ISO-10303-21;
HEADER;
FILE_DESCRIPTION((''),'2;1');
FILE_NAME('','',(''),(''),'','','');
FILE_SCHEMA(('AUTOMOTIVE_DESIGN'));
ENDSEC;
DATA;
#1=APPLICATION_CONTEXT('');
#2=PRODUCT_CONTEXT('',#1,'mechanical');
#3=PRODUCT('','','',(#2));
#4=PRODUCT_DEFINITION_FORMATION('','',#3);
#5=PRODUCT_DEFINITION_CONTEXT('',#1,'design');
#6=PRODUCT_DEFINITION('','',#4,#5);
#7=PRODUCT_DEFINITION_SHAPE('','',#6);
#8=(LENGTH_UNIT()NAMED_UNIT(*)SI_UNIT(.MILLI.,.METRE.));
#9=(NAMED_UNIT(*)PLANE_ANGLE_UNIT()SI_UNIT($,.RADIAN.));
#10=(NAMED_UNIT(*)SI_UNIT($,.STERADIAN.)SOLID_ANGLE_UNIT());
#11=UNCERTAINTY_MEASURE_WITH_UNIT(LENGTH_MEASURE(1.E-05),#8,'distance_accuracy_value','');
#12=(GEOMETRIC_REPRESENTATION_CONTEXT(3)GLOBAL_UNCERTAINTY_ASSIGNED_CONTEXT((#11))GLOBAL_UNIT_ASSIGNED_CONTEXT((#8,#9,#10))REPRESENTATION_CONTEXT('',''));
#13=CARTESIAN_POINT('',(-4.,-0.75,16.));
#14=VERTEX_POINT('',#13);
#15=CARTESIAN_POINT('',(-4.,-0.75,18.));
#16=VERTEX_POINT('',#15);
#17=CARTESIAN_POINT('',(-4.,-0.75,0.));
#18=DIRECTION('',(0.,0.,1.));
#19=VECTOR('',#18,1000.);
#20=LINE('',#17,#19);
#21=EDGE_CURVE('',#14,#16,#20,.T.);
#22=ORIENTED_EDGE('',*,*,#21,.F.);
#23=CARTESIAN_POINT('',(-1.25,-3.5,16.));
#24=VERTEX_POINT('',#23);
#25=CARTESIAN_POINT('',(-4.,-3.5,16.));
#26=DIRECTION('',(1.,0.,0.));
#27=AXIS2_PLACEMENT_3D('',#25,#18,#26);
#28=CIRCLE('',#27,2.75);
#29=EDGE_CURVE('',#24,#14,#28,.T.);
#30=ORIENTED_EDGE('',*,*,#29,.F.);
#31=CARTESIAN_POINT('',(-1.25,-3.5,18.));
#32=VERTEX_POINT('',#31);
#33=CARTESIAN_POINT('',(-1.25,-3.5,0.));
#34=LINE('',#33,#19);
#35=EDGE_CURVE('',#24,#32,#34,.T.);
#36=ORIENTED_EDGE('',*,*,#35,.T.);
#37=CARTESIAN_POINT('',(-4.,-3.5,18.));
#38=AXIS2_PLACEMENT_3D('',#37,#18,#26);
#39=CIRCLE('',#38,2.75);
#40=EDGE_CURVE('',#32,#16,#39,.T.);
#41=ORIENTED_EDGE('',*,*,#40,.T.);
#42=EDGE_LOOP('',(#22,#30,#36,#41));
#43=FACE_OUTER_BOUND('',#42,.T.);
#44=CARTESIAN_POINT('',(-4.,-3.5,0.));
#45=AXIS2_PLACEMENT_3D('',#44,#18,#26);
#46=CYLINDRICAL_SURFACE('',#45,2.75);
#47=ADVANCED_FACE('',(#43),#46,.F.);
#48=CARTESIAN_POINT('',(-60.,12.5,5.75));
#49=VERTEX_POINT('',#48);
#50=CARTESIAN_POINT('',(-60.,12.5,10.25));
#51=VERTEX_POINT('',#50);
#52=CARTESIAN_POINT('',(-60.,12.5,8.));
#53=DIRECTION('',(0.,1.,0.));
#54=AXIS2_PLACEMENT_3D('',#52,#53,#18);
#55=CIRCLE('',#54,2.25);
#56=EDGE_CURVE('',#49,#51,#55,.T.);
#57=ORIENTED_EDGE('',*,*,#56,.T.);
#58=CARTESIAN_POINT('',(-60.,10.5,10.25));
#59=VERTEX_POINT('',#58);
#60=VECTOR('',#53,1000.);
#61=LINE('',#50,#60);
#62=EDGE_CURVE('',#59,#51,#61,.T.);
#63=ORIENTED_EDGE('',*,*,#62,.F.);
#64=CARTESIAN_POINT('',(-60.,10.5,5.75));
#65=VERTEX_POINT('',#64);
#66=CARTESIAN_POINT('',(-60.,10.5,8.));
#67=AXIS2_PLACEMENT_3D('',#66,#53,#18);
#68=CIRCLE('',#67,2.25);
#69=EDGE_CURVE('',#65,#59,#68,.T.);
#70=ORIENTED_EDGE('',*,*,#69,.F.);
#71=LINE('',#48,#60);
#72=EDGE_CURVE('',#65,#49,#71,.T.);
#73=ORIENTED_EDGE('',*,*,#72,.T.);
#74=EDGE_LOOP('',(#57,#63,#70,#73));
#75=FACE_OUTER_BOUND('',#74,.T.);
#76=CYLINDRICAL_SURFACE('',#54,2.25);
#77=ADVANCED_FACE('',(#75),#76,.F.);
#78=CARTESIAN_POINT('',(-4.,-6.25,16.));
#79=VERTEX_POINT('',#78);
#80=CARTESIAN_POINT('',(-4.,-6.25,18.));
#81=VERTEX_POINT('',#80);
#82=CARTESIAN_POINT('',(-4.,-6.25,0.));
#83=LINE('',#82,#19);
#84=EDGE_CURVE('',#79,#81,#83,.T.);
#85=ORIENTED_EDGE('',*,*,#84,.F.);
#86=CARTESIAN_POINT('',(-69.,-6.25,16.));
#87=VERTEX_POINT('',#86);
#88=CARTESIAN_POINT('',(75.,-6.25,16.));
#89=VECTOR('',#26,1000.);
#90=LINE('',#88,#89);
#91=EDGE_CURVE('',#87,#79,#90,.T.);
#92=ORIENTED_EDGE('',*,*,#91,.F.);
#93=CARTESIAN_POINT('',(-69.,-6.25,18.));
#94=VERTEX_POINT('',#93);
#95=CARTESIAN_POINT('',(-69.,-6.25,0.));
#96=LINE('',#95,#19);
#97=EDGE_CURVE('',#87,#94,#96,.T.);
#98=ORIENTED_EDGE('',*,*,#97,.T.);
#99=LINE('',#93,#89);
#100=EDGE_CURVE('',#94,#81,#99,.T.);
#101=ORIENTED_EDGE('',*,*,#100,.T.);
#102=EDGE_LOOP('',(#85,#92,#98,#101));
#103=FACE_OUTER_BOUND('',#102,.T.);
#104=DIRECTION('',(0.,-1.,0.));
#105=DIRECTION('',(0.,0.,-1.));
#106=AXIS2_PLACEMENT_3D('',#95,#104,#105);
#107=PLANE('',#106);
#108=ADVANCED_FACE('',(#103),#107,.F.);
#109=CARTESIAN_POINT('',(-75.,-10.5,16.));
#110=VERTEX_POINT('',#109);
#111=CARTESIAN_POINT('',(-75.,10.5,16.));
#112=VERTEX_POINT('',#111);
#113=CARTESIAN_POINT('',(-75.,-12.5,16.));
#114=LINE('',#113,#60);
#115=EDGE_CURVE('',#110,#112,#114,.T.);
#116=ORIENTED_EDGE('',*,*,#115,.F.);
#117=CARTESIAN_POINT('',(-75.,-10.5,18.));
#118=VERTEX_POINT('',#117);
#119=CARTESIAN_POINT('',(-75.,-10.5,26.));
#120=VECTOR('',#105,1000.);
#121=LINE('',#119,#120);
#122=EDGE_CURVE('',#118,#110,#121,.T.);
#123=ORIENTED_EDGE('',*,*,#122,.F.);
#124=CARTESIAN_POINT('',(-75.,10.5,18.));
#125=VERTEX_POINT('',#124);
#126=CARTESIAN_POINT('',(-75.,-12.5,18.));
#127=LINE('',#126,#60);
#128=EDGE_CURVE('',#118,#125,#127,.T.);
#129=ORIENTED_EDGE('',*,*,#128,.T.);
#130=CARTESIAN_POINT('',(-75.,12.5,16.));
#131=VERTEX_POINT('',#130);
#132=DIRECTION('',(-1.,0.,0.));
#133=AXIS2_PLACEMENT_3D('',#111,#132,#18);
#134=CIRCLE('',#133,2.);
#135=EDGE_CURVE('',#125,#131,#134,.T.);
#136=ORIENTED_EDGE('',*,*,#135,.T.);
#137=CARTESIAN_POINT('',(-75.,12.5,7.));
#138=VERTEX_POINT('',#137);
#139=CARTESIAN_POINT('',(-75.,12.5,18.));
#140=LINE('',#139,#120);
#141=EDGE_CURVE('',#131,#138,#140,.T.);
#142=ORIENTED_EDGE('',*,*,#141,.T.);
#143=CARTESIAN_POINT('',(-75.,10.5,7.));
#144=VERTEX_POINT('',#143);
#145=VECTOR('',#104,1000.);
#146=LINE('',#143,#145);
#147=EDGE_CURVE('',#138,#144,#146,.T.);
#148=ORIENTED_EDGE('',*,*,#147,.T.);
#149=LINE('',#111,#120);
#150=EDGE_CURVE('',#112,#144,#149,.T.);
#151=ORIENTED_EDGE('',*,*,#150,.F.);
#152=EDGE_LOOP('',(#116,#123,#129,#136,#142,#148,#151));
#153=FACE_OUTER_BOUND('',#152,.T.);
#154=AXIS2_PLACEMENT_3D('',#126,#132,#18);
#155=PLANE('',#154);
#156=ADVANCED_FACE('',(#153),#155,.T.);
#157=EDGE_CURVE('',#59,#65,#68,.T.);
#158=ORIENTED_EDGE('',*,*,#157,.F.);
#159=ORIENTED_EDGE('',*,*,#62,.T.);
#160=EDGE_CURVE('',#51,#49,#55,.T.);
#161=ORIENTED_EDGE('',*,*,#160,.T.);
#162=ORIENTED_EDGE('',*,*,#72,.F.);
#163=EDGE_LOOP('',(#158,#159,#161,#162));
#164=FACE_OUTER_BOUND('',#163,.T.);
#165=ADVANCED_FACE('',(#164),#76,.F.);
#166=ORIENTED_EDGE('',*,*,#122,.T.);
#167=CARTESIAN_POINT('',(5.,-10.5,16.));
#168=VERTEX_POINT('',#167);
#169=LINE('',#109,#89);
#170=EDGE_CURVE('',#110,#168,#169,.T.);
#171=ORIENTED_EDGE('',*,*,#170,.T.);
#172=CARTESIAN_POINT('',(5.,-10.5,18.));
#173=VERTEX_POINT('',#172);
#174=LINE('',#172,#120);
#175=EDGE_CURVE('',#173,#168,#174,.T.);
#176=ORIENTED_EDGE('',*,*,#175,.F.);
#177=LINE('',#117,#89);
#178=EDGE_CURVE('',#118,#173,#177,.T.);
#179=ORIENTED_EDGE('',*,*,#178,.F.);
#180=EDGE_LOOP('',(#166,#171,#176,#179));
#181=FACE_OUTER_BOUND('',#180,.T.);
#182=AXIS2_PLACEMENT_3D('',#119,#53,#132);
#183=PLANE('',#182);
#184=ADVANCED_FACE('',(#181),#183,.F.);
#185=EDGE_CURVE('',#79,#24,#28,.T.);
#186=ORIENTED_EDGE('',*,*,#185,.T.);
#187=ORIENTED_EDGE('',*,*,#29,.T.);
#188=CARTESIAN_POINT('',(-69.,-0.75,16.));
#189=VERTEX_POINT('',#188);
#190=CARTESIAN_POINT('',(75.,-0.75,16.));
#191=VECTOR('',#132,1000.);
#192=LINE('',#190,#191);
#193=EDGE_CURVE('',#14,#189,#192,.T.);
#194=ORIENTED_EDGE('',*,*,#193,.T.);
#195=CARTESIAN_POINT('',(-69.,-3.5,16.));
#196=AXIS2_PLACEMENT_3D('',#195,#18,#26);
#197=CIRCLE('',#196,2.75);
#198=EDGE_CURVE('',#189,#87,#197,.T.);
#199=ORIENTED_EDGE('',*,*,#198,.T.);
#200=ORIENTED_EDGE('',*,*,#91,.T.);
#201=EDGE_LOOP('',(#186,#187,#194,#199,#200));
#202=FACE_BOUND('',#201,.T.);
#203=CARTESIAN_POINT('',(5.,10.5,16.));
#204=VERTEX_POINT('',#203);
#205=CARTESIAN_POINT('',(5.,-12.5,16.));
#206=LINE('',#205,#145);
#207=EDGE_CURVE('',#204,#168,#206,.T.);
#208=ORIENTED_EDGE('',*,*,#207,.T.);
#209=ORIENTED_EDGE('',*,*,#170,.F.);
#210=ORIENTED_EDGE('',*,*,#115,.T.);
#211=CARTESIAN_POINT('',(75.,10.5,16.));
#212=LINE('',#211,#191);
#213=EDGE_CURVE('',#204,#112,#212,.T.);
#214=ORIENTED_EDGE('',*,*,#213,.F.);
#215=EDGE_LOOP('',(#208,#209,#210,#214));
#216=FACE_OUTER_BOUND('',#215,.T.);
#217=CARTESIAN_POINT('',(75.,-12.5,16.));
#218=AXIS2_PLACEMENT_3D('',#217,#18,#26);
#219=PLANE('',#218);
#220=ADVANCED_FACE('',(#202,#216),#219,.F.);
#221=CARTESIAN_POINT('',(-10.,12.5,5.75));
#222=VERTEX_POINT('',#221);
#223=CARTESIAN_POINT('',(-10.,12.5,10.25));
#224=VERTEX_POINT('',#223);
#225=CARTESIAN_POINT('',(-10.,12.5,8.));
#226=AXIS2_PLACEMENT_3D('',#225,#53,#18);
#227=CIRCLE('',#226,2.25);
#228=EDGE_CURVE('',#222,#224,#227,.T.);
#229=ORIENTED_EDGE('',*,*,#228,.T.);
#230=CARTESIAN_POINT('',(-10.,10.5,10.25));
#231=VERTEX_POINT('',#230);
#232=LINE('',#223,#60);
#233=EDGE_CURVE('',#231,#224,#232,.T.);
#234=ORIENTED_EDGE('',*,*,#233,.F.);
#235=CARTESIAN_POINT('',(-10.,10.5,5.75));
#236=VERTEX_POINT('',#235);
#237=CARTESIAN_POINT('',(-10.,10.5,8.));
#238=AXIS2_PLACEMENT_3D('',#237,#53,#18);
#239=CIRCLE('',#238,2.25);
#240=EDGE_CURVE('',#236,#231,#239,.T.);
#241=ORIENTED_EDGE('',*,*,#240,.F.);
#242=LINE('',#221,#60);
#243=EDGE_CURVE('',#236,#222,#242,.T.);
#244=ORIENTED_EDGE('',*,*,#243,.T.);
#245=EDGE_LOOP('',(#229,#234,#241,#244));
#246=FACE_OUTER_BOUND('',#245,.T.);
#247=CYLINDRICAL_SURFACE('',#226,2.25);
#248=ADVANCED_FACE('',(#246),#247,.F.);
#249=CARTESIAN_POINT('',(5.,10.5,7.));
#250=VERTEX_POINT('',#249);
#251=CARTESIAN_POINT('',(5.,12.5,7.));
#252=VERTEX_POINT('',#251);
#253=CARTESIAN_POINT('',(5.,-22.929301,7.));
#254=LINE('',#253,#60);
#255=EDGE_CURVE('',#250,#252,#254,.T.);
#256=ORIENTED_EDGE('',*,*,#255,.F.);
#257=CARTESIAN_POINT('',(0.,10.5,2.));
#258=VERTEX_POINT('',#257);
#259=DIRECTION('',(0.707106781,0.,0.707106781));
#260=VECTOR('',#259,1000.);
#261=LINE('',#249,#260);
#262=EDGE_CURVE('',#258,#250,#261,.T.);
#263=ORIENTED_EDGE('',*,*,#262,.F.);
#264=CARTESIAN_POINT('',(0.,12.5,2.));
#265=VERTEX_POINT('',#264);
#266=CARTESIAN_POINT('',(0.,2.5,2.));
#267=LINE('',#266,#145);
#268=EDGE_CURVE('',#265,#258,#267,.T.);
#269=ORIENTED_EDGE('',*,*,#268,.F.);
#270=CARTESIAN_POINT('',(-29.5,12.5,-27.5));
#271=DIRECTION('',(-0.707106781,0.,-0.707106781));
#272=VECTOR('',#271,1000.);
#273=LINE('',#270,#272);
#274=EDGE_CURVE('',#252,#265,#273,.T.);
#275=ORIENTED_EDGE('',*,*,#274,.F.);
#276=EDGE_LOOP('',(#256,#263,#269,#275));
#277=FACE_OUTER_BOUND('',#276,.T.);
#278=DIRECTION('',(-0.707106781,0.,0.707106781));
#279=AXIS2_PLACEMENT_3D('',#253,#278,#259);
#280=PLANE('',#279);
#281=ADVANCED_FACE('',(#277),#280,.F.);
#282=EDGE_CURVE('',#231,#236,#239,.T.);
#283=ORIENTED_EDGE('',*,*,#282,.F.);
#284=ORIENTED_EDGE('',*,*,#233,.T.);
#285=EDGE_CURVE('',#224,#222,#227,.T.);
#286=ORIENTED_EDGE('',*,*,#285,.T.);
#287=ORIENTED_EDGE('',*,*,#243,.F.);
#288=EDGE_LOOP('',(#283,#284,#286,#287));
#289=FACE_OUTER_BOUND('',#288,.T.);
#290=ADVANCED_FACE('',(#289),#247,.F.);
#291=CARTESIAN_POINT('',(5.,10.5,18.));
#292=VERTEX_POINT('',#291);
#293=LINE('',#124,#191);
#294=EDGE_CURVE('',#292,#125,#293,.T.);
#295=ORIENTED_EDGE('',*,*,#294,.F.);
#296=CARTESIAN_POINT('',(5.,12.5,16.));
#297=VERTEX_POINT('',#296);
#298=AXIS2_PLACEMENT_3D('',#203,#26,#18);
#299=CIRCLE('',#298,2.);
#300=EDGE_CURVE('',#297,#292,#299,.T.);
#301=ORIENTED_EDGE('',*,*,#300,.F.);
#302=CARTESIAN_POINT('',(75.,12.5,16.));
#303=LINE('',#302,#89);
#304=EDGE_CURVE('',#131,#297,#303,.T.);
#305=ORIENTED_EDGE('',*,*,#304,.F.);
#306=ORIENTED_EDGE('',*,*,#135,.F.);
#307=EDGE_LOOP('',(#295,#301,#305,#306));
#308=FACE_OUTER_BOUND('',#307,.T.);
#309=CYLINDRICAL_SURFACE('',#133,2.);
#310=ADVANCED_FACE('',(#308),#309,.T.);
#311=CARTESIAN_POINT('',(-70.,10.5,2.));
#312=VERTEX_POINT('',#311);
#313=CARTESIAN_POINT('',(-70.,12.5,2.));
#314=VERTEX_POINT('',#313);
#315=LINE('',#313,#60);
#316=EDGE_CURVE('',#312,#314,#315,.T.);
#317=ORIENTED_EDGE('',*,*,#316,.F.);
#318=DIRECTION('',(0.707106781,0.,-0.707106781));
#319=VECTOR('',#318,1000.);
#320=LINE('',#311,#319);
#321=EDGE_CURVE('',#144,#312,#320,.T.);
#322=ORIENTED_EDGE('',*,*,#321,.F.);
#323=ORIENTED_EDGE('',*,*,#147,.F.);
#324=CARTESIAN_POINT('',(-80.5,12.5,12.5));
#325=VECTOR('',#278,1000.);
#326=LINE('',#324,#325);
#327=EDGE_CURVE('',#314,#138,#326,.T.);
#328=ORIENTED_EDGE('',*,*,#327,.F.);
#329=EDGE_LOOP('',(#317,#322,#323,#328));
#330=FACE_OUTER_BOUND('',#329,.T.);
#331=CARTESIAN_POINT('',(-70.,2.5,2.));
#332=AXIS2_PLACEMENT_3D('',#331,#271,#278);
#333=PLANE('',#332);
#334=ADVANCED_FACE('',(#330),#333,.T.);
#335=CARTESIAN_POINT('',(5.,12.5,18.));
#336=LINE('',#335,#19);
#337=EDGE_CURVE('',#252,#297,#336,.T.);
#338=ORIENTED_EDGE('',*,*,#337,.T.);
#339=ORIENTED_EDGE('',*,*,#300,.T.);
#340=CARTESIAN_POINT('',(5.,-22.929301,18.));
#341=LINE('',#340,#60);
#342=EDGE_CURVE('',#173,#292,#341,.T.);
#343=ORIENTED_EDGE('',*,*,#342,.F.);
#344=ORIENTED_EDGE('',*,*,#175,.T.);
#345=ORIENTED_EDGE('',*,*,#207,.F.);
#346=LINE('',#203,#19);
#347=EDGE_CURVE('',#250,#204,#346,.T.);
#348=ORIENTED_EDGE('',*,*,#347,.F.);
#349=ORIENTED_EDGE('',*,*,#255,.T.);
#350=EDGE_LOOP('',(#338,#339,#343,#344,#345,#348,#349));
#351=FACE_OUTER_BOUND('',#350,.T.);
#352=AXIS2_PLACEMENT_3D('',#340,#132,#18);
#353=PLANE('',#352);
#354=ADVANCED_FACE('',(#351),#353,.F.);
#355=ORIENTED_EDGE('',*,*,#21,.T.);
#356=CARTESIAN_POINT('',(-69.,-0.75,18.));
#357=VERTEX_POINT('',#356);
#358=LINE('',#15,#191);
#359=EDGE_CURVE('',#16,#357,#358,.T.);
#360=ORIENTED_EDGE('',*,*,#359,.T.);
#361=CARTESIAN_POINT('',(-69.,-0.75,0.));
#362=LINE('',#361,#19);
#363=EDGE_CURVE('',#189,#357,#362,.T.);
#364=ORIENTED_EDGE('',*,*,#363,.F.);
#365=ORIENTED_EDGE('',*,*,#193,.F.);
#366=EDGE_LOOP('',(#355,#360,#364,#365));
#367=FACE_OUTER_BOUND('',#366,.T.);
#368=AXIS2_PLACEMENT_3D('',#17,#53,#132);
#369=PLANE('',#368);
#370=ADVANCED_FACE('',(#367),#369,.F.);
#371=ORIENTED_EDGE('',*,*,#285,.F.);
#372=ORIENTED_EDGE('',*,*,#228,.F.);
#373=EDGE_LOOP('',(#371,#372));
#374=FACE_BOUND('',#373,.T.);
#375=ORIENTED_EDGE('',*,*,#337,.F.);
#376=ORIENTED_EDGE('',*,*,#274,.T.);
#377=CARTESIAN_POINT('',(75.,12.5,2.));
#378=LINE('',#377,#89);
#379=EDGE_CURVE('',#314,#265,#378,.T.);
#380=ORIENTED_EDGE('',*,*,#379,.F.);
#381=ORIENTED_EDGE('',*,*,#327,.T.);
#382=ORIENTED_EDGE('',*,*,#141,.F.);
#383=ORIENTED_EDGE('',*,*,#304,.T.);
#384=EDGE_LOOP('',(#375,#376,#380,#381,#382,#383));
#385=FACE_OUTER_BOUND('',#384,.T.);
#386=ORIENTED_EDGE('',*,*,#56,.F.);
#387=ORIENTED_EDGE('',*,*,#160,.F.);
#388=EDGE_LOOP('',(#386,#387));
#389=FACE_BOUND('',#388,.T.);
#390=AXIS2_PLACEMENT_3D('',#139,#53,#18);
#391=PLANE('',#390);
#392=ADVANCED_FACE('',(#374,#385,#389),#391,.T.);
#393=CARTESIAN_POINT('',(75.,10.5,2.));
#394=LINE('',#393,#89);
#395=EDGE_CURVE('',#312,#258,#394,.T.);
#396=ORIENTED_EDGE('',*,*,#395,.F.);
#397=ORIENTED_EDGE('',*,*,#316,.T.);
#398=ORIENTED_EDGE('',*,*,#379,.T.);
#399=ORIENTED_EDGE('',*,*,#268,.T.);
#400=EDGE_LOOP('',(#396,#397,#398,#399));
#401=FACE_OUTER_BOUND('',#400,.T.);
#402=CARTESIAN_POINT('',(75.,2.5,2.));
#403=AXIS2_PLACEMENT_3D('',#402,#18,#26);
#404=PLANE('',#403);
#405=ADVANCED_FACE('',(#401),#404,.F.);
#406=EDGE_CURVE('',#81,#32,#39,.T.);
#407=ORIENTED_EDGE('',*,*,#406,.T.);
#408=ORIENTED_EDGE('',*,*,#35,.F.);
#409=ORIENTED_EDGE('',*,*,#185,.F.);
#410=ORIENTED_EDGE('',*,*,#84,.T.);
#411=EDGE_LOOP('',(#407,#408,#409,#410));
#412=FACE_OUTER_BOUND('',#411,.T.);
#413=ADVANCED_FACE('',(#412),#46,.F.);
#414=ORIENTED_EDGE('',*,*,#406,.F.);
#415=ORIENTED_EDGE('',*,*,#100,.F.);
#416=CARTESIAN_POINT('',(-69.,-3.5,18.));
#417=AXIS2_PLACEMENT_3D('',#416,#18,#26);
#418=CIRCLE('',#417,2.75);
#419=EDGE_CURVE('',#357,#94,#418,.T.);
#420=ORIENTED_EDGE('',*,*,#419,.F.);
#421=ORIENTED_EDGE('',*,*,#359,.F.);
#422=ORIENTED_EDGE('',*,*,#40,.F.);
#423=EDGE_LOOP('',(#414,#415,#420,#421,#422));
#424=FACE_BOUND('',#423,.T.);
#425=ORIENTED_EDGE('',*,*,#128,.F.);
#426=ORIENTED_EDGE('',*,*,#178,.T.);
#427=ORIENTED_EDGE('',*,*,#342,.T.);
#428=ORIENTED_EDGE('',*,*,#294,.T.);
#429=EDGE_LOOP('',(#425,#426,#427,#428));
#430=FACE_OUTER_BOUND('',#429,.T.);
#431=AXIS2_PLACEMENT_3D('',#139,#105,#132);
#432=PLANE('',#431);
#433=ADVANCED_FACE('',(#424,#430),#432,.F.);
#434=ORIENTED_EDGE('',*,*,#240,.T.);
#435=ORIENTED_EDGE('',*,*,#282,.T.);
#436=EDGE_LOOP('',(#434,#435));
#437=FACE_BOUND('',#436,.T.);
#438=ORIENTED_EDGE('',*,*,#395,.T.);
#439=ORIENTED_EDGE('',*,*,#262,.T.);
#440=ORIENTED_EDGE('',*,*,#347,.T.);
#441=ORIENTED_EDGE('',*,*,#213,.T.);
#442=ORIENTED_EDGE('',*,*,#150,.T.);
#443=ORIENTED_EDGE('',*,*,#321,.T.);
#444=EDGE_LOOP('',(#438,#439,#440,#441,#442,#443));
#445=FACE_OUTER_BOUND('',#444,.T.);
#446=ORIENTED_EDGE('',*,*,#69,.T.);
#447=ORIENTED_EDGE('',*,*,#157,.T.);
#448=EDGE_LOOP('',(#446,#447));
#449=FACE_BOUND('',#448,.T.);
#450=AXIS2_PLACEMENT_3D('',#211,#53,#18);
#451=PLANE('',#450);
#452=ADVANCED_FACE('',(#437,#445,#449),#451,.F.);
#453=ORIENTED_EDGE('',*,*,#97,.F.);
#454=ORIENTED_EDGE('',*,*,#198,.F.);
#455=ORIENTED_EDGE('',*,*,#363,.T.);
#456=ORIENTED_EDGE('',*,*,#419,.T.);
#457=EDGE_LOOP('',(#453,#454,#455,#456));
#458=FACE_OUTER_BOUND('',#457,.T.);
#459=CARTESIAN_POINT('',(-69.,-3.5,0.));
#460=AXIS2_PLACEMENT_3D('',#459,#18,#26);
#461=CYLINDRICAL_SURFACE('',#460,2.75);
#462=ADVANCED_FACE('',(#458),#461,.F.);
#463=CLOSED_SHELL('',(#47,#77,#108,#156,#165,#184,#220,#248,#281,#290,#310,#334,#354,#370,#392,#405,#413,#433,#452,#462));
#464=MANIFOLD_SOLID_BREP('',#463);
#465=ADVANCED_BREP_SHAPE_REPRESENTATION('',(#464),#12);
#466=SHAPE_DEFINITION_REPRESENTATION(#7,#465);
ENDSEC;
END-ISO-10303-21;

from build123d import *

# Parameters (mm, degrees)
SKETCH_1_W             = 150
SKETCH_1_H             = 25
BOSS_EXTRUDE_1_DEPTH   = 18
SKETCH_2_W             = 16
SKETCH_2_H             = 23
CUT_EXTRUDE_1_DEPTH    = 152.592381075
CUT_EXTRUDE_3_DEPTH    = 79.136099212
F_4_5_4_5_HOLE_1_D     = 4.5
F_4_5_4_5_HOLE_1_DEPTH = 15
F_4_5_4_5_HOLE_1_TIP   = 1.351936393
F_4_5_4_5_HOLE_3_D     = 4.5
F_4_5_4_5_HOLE_3_DEPTH = 15
F_4_5_4_5_HOLE_3_TIP   = 1.351936393
F_4_5_4_5_HOLE_2_D     = 4.5
F_4_5_4_5_HOLE_2_DEPTH = 15
F_4_5_4_5_HOLE_2_TIP   = 1.351936393
CHAMFER_1_SIZE         = 2
FILLET_1_R             = 2
SKETCH_11_W            = 150
SKETCH_11_H            = 2
CUT_EXTRUDE_4_DEPTH    = 10
CHAMFER_4_SIZE         = 5
SKETCH_12_W            = 121.932032981
SKETCH_12_H            = 48.36827262
CUT_EXTRUDE_5_DEPTH    = 78.699742599
CHAMFER_5_SIZE         = 5
SKETCH_13_W            = 80
SKETCH_13_H            = 2
CUT_EXTRUDE_6_DEPTH    = 10


with BuildPart() as part:
    # Sketch 1 → Boss-Extrude 1 (new body)
    with BuildSketch(Plane(origin=(0, 0, 0), x_dir=(-1, 0, 0), z_dir=(0, 0, -1))):
        Rectangle(SKETCH_1_W, SKETCH_1_H)
    extrude(amount=-BOSS_EXTRUDE_1_DEPTH)

    # Sketch 2 → Cut-Extrude 1 (cut, through all)
    with BuildSketch(Plane.ZY.offset(75)):
        with Locations((8, -1)):
            Rectangle(SKETCH_2_W, SKETCH_2_H)
    extrude(amount=-CUT_EXTRUDE_1_DEPTH, mode=Mode.SUBTRACT)

    # Sketch 4 → Cut-Extrude 3 (cut, through all)
    with BuildSketch(Plane.XY.offset(18)):
        with BuildLine():
            Line((-69, -6.25), (-4, -6.25))
            ThreePointArc((-4, -6.25), (-1.25, -3.5), (-4, -0.75))
            Line((-4, -0.75), (-69, -0.75))
            ThreePointArc((-69, -0.75), (-71.75, -3.5), (-69, -6.25))
        make_face()
    extrude(amount=-CUT_EXTRUDE_3_DEPTH, mode=Mode.SUBTRACT)

    # Ø4.5 (4.5) Hole 1
    with Locations(Plane(origin=(0, 12.5, 0), x_dir=(-1, 0, 0), z_dir=(0, 1, 0))):
        with Locations((-60, 8)):
            Hole(F_4_5_4_5_HOLE_1_D / 2, depth=F_4_5_4_5_HOLE_1_DEPTH)
            with Locations((0, 0, -(F_4_5_4_5_HOLE_1_DEPTH + F_4_5_4_5_HOLE_1_TIP / 2))):  # 118° drill point
                Cone(0, F_4_5_4_5_HOLE_1_D / 2, F_4_5_4_5_HOLE_1_TIP, mode=Mode.SUBTRACT)

    # Ø4.5 (4.5) Hole 3
    with Locations(Plane(origin=(0, 12.5, 0), x_dir=(-1, 0, 0), z_dir=(0, 1, 0))):
        with Locations((60, 8)):
            Hole(F_4_5_4_5_HOLE_3_D / 2, depth=F_4_5_4_5_HOLE_3_DEPTH)
            with Locations((0, 0, -(F_4_5_4_5_HOLE_3_DEPTH + F_4_5_4_5_HOLE_3_TIP / 2))):  # 118° drill point
                Cone(0, F_4_5_4_5_HOLE_3_D / 2, F_4_5_4_5_HOLE_3_TIP, mode=Mode.SUBTRACT)

    # Ø4.5 (4.5) Hole 2
    with Locations(Plane(origin=(0, 12.5, 0), x_dir=(-1, 0, 0), z_dir=(0, 1, 0))):
        with Locations((10, 8)):
            Hole(F_4_5_4_5_HOLE_2_D / 2, depth=F_4_5_4_5_HOLE_2_DEPTH)
            with Locations((0, 0, -(F_4_5_4_5_HOLE_2_DEPTH + F_4_5_4_5_HOLE_2_TIP / 2))):  # 118° drill point
                Cone(0, F_4_5_4_5_HOLE_2_D / 2, F_4_5_4_5_HOLE_2_TIP, mode=Mode.SUBTRACT)

    # Chamfer 1
    chamfer_1_edges = [part.edges().sort_by_distance(p)[0] for p in [
        (75, -12.5, 17),
    ]]
    chamfer(chamfer_1_edges, length=CHAMFER_1_SIZE)

    # Fillet 1
    fillet_1_edges = [part.edges().sort_by_distance(p)[0] for p in [
        (0, 12.5, 18),
    ]]
    fillet(fillet_1_edges, radius=FILLET_1_R)

    # Sketch 11 → Cut-Extrude 4 (cut)
    with BuildSketch(Plane(origin=(0, 12.5, 0), x_dir=(1, 0, 0), z_dir=(0, 1, 0))):
        with Locations((0, -1)):
            Rectangle(SKETCH_11_W, SKETCH_11_H)
    extrude(amount=-CUT_EXTRUDE_4_DEPTH, mode=Mode.SUBTRACT)

    # Chamfer 4
    chamfer_4_edges = [part.edges().sort_by_distance(p)[0] for p in [
        (75, 11.5, 2),
        (-75, 11.5, 2),
    ]]
    chamfer(chamfer_4_edges, length=CHAMFER_4_SIZE)

    # Sketch 12 → Cut-Extrude 5 (cut, through all)
    with BuildSketch(Plane(origin=(0, 0, 2), x_dir=(-1, 0, 0), z_dir=(0, 0, -1))):
        with Locations((-65.966016491, 1.254835332)):
            Rectangle(SKETCH_12_W, SKETCH_12_H)
    extrude(amount=-CUT_EXTRUDE_5_DEPTH, mode=Mode.SUBTRACT)

    # Chamfer 5
    chamfer_5_edges = [part.edges().sort_by_distance(p)[0] for p in [
        (5, 11.5, 2),
    ]]
    chamfer(chamfer_5_edges, length=CHAMFER_5_SIZE)

    # Sketch 13 → Cut-Extrude 6 (cut)
    with BuildSketch(Plane(origin=(0, 0, 16), x_dir=(-1, 0, 0), z_dir=(0, 0, -1))):
        with Locations((35, -11.5)):
            Rectangle(SKETCH_13_W, SKETCH_13_H)
    extrude(amount=-CUT_EXTRUDE_6_DEPTH, mode=Mode.SUBTRACT)


solid = part.part
